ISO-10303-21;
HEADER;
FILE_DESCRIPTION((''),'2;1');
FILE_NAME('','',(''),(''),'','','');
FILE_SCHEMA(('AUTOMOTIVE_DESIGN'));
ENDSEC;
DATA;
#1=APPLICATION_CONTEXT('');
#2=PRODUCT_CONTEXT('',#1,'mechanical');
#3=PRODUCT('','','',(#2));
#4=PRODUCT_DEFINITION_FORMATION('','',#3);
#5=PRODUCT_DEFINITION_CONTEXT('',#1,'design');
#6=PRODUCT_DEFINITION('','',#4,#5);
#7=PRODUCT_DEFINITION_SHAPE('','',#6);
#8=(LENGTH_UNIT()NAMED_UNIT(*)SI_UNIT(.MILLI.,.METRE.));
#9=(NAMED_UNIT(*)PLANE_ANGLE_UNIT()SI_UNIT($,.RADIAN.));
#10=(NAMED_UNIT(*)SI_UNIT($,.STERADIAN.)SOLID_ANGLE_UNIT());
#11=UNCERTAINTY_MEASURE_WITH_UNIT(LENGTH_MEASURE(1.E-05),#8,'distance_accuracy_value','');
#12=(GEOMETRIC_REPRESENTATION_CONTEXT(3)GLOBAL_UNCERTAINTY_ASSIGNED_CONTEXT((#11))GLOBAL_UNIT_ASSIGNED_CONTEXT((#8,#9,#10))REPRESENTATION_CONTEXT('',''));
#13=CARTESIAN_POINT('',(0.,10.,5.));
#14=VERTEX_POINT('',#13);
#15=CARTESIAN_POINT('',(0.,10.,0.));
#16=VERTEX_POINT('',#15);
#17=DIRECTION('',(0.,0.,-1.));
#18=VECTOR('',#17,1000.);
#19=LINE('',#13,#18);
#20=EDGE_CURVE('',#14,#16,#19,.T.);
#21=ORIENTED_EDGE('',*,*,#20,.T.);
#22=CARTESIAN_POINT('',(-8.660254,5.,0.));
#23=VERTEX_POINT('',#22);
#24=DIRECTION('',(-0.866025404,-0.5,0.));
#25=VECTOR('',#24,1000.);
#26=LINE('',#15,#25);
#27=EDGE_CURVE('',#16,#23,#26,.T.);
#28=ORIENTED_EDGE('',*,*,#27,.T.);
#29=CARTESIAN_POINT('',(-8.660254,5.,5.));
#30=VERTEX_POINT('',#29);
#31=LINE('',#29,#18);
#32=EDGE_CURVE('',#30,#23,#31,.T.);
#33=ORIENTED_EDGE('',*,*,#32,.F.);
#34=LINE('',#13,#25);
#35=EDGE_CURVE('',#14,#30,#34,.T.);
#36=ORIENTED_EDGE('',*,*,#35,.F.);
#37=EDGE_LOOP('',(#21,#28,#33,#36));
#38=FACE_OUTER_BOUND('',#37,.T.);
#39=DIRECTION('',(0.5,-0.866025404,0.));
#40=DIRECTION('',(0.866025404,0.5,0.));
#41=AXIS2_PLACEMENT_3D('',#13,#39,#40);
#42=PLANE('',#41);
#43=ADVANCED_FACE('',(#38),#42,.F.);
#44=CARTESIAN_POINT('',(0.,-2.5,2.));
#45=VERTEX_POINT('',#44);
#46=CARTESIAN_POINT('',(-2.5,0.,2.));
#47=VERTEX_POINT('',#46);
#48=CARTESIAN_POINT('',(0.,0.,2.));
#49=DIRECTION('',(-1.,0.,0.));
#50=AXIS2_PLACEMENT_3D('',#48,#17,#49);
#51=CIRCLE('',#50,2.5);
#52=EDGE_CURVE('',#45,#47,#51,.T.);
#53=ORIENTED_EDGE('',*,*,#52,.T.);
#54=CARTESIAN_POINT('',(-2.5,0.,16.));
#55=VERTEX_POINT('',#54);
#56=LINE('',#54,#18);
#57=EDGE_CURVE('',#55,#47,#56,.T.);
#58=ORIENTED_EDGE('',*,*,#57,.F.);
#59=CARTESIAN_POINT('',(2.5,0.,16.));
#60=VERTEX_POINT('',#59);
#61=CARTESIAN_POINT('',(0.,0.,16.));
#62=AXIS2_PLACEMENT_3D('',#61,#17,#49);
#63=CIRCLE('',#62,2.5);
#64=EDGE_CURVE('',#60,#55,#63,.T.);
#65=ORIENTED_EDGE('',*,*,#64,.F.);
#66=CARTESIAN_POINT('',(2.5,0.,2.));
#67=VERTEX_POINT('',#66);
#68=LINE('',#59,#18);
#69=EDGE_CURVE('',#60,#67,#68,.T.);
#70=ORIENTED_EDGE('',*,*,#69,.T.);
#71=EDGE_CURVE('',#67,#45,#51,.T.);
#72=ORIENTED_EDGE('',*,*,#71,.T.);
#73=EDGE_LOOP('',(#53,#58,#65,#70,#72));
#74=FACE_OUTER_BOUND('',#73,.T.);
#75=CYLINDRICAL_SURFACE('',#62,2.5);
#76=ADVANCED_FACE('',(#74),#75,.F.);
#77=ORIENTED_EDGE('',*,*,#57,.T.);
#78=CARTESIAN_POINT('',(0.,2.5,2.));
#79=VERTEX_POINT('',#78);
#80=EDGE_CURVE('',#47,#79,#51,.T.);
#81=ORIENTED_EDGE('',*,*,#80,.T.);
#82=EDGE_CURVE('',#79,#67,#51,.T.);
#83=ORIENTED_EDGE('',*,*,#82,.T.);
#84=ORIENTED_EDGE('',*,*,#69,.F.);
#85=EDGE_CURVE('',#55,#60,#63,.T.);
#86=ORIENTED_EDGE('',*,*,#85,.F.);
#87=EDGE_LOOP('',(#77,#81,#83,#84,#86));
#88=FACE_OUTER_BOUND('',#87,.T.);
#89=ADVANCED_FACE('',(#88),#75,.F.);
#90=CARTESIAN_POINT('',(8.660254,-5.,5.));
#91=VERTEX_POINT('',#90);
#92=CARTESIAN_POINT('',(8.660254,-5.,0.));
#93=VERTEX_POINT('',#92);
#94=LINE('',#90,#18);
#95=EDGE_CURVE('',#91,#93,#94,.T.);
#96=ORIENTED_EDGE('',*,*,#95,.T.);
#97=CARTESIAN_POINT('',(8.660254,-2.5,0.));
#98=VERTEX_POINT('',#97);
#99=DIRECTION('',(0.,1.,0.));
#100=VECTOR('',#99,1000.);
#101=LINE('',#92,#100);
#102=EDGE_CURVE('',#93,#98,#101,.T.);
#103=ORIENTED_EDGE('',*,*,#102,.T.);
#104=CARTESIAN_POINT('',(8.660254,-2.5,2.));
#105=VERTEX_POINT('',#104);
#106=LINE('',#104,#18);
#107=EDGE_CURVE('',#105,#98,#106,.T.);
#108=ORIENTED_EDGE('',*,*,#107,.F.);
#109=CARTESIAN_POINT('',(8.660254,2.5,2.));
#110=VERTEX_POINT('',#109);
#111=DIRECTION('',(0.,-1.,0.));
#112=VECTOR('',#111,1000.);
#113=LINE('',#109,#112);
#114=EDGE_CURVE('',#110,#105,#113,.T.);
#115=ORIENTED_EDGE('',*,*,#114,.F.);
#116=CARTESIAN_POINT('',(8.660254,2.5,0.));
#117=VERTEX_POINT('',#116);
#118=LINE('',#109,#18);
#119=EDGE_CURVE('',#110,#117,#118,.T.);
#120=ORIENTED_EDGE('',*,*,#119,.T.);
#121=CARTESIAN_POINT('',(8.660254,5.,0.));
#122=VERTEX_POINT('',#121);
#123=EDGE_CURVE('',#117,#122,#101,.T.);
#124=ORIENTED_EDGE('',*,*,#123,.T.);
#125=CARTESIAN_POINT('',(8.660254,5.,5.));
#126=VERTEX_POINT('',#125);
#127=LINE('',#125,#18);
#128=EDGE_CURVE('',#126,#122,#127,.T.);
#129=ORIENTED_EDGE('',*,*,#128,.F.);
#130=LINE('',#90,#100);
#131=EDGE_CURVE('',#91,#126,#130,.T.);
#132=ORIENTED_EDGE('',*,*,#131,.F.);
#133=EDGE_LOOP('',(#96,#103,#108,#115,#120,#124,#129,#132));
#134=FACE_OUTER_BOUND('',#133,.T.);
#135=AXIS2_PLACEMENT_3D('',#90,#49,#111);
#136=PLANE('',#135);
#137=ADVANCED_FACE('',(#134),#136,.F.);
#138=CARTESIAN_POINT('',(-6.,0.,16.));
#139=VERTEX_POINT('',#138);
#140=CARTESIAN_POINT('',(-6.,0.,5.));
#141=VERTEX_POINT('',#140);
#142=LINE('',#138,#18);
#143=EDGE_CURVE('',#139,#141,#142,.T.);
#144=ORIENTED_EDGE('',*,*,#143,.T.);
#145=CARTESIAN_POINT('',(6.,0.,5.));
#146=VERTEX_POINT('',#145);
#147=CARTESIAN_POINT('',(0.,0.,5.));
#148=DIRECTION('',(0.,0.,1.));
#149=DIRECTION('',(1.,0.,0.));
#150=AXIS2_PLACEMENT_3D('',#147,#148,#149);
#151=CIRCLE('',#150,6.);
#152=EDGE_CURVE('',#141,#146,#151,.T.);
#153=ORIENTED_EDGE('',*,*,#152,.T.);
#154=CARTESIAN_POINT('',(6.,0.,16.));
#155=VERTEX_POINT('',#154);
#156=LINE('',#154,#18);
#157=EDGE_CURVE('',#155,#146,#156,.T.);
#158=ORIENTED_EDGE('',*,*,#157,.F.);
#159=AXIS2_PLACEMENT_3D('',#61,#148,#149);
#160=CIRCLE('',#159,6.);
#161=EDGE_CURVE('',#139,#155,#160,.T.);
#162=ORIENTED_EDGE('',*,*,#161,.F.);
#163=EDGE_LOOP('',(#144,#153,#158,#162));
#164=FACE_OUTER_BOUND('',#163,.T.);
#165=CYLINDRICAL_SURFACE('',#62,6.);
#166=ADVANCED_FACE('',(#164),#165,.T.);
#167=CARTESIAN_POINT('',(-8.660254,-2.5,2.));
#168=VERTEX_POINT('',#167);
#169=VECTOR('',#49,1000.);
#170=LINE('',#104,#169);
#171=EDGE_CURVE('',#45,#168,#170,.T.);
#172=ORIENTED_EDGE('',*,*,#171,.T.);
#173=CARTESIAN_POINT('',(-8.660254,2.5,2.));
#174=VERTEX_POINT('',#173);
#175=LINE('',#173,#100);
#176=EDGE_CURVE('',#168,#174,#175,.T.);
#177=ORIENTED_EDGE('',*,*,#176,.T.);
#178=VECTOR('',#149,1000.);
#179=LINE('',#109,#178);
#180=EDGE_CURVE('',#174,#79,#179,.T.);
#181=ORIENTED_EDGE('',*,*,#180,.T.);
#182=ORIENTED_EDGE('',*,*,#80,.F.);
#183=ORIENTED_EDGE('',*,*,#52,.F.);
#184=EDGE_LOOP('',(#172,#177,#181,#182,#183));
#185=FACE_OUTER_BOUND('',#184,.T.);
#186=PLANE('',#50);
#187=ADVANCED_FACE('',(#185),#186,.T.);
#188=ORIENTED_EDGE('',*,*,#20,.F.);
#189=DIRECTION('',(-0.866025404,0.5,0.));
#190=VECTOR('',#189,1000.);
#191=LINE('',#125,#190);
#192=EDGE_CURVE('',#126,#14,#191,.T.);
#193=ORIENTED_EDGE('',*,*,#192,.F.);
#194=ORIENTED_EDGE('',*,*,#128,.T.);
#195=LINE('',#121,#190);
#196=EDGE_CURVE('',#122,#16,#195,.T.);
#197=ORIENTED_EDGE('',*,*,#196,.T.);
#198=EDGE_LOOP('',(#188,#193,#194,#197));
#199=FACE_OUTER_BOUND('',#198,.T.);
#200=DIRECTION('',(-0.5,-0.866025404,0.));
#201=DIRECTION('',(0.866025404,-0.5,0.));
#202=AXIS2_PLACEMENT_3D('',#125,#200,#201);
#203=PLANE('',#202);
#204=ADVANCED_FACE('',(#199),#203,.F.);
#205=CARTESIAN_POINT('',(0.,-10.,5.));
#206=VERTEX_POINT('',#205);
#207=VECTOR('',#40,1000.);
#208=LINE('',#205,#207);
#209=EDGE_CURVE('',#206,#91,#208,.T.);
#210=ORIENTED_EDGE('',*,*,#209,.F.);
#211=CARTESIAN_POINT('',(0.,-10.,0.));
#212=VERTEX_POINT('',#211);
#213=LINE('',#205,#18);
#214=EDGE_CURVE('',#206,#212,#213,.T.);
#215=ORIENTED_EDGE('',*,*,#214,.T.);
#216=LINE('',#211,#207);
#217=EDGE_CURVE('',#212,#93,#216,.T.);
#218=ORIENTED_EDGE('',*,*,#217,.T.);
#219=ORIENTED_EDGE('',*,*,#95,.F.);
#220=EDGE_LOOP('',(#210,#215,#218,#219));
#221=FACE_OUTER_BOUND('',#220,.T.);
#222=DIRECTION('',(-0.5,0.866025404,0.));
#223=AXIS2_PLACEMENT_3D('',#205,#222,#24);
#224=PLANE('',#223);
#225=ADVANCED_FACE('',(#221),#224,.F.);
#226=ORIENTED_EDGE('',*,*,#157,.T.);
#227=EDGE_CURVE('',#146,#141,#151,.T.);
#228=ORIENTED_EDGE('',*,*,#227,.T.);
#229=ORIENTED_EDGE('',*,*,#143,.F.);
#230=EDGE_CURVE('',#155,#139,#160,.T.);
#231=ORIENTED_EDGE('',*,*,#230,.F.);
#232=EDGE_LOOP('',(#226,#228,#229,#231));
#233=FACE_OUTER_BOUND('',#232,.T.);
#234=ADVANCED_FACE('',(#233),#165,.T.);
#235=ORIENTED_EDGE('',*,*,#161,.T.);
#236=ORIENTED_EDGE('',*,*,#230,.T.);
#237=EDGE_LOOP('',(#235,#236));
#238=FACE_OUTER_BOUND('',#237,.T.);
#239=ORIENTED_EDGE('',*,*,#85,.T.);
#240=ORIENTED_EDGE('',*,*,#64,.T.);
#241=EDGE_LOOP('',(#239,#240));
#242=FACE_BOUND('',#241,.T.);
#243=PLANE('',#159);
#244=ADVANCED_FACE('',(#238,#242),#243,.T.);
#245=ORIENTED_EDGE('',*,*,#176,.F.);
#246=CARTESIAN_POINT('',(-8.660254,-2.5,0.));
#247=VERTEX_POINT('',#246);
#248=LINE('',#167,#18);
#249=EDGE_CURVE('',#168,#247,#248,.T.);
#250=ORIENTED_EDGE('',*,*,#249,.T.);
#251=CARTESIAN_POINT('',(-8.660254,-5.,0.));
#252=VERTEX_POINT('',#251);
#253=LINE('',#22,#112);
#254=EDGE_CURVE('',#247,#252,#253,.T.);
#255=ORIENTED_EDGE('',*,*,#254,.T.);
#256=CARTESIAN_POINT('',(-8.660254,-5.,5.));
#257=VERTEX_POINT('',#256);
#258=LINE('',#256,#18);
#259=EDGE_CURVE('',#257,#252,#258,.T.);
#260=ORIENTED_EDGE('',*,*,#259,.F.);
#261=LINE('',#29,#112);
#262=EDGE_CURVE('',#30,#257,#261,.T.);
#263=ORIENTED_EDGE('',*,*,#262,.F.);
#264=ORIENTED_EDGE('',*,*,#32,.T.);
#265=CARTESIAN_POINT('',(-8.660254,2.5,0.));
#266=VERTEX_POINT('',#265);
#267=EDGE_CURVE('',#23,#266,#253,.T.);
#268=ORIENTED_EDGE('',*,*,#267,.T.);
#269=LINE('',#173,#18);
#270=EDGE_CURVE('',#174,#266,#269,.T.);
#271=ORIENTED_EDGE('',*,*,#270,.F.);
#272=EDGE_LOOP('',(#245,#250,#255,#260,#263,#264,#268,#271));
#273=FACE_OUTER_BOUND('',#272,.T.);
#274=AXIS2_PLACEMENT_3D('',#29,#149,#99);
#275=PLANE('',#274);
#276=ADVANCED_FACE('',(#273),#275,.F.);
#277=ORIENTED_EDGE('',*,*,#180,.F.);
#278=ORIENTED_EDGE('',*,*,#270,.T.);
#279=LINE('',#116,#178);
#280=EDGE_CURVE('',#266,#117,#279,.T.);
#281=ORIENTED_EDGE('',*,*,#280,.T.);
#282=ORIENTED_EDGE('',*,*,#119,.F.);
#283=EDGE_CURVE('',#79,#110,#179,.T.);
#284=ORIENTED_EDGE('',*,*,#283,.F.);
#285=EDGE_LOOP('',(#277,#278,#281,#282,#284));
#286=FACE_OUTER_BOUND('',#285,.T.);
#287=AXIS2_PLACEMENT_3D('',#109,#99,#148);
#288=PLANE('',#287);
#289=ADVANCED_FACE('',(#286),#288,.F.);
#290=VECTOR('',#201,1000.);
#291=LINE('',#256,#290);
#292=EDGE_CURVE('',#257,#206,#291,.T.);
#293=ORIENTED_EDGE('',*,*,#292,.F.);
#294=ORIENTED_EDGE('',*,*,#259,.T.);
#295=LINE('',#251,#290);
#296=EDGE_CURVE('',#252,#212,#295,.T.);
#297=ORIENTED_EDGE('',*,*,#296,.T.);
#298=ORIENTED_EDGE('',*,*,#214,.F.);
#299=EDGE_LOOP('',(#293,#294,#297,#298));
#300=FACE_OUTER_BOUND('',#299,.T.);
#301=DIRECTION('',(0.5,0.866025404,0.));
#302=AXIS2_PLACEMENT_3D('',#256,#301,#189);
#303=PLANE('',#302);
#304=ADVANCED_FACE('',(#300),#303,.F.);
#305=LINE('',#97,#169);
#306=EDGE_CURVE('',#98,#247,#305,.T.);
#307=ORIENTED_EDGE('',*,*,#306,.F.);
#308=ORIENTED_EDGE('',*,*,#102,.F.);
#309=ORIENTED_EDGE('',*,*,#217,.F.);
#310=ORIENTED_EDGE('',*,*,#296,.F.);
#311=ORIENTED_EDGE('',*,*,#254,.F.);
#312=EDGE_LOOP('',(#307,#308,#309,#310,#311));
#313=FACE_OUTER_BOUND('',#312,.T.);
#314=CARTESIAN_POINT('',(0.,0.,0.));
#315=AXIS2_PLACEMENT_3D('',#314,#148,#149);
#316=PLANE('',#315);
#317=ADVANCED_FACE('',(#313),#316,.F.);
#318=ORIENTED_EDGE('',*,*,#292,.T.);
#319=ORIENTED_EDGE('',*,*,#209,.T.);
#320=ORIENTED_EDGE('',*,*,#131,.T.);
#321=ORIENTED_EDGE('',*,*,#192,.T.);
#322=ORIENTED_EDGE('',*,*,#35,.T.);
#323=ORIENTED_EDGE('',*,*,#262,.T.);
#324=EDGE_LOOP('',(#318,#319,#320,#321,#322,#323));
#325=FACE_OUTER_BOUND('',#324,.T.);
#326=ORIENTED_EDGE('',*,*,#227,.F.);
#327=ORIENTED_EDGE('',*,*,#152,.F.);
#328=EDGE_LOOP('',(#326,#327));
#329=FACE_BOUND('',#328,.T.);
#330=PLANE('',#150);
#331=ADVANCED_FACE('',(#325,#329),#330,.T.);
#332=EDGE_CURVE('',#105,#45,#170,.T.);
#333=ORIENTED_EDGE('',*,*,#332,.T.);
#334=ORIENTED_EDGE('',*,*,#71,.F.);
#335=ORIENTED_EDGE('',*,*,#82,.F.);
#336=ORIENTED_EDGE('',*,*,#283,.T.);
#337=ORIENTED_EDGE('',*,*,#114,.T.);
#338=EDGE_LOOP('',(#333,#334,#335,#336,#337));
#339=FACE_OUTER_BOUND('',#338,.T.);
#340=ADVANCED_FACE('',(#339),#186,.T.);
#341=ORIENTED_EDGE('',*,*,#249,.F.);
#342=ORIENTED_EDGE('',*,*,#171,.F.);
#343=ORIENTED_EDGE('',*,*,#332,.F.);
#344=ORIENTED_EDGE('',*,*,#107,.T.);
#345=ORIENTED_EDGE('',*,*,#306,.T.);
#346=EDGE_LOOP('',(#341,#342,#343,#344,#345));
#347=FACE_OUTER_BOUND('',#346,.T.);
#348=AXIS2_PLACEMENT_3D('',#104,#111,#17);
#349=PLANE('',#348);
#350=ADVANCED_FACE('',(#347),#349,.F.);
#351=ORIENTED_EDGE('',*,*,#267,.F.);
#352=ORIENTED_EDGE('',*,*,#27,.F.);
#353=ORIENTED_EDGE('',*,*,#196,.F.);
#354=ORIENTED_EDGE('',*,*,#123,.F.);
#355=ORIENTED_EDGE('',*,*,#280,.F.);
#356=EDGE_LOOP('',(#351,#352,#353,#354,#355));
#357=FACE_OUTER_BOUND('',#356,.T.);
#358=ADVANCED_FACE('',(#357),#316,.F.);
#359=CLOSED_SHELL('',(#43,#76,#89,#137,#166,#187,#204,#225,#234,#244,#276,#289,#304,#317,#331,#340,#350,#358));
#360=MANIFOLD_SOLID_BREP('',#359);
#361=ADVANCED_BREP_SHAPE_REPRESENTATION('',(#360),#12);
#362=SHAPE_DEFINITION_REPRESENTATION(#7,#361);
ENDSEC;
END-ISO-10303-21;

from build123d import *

# Parameters (mm, degrees)
HEX_FLANGE_DEPTH          = 5
BOSS_SKETCH_12_R          = 6
CYLINDRICAL_BOSS_12_DEPTH = 11
FLANGE_SLOT_SKETCH_W      = 17.320508076
FLANGE_SLOT_SKETCH_H      = 5
FLANGE_SLOT_CUT_DEPTH     = 2
BORE_SKETCH_5_R           = 2.5
BORE_5_DEPTH              = 20.261360284


with BuildPart() as part:
    # Hex Flange Sketch → Hex Flange (new body)
    with BuildSketch(Plane.XY):
        Polygon((0, 10), (-8.660254038, 5), (-8.660254038, -5), (0, -10), (8.660254038, -5), (8.660254038, 5), align=None)
    extrude(amount=HEX_FLANGE_DEPTH)

    # Boss Sketch Ø12 → Cylindrical Boss Ø12 (add)
    with BuildSketch(Plane.XY.offset(5)):
        Circle(BOSS_SKETCH_12_R)
    extrude(amount=CYLINDRICAL_BOSS_12_DEPTH)

    # Flange Slot Sketch → Flange Slot Cut (cut)
    with BuildSketch(Plane(origin=(0, 0, 0), x_dir=(-1, 0, 0), z_dir=(0, 0, -1))):
        Rectangle(FLANGE_SLOT_SKETCH_W, FLANGE_SLOT_SKETCH_H)
    extrude(amount=-FLANGE_SLOT_CUT_DEPTH, mode=Mode.SUBTRACT)

    # Bore Sketch Ø5 → Bore Ø5 (cut, through all)
    with BuildSketch(Plane(origin=(0, 0, 2), x_dir=(-1, 0, 0), z_dir=(0, 0, -1))):
        Circle(BORE_SKETCH_5_R)
    extrude(amount=-BORE_5_DEPTH, mode=Mode.SUBTRACT)


solid = part.part
